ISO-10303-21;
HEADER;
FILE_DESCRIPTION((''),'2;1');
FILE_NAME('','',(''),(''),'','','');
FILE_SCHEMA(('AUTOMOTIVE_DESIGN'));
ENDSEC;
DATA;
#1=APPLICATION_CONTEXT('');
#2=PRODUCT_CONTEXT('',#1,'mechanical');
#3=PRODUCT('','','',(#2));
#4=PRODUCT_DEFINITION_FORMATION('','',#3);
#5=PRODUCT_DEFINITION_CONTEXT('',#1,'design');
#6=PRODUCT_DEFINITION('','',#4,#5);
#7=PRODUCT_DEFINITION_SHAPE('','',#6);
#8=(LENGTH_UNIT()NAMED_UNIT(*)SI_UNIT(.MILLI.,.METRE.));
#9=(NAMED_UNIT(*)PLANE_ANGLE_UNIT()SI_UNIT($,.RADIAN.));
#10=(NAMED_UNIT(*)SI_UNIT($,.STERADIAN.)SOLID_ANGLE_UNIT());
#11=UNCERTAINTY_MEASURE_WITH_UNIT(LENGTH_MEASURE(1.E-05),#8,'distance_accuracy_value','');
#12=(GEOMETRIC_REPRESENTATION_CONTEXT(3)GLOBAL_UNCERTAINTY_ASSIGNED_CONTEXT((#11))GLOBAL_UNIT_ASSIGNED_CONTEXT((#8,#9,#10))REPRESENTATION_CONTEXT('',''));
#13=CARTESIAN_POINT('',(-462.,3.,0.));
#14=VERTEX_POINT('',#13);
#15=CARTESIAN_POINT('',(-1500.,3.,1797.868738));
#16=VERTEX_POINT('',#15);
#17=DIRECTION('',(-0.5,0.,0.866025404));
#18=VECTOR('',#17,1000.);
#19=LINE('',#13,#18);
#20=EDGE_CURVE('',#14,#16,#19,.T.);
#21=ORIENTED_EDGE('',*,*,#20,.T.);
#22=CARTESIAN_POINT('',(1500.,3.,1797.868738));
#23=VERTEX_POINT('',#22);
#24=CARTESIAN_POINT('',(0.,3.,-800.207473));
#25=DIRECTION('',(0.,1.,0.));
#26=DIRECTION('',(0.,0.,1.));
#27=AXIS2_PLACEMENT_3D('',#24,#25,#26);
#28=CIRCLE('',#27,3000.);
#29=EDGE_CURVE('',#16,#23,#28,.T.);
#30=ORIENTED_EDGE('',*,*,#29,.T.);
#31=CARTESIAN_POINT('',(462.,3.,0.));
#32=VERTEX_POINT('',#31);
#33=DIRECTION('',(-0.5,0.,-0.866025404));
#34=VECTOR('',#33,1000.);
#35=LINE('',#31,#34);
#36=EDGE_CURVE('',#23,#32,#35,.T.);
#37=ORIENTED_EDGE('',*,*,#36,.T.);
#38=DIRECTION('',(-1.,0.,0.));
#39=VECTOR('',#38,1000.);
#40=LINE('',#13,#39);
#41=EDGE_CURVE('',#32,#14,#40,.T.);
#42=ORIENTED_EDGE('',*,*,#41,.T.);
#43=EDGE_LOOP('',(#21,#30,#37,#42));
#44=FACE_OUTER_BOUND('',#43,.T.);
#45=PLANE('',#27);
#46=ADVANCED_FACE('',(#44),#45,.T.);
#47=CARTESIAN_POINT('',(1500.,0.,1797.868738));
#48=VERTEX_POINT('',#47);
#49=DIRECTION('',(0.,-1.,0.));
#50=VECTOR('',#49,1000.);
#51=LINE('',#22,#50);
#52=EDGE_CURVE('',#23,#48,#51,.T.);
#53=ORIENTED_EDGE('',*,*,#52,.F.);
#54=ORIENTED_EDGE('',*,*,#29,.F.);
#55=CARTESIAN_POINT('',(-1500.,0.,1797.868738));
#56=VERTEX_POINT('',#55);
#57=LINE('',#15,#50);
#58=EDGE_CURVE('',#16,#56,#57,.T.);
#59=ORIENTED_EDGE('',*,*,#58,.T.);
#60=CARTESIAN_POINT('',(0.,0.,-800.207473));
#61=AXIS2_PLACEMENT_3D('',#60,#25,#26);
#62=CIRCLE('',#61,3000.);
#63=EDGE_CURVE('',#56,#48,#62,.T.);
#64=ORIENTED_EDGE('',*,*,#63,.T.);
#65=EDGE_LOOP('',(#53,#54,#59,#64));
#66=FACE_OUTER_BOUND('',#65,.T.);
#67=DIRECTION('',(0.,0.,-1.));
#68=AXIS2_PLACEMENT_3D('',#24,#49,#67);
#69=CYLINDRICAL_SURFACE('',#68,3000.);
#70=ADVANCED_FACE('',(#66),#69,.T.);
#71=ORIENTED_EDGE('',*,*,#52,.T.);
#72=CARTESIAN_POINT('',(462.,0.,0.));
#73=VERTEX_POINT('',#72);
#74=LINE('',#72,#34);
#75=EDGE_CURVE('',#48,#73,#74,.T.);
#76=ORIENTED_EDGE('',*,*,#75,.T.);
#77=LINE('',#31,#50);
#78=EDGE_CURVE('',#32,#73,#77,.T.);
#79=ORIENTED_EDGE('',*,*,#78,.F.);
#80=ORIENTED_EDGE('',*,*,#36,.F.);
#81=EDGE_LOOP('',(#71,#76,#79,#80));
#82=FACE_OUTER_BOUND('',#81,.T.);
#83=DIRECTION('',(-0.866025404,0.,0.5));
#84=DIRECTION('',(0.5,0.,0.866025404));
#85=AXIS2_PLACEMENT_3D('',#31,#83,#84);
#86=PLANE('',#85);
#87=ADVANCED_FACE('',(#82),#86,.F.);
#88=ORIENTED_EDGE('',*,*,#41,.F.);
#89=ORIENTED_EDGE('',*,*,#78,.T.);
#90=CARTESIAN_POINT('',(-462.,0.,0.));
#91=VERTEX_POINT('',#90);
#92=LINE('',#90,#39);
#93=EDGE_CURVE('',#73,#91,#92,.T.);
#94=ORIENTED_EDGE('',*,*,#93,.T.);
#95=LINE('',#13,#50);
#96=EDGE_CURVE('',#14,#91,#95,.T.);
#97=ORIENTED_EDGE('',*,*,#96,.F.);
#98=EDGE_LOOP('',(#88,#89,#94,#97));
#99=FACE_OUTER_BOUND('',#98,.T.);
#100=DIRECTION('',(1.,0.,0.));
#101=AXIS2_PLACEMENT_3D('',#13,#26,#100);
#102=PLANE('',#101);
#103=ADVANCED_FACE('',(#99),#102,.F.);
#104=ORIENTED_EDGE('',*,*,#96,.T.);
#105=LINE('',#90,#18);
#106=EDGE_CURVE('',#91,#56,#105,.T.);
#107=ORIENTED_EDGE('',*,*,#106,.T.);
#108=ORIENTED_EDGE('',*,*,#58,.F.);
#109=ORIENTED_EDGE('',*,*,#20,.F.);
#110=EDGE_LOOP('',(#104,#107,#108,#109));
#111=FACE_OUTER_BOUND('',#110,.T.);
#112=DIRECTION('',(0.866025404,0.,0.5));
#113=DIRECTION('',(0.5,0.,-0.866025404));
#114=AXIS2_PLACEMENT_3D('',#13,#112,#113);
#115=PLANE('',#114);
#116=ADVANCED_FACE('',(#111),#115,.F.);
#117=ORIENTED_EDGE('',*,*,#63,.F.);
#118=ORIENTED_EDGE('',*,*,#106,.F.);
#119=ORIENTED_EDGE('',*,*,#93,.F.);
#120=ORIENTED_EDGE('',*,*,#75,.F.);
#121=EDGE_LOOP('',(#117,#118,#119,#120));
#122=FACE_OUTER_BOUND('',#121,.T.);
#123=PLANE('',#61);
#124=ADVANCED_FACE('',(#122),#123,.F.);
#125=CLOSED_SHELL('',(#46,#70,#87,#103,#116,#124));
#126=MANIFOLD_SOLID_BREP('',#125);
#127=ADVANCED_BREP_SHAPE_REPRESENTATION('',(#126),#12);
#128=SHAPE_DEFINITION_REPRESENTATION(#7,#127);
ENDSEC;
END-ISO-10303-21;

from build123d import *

# Parameters (mm, degrees)
BOSS_EXTRUDE1_DEPTH = 3


with BuildPart() as part:
    # Sketch1 → Boss-Extrude1 (new body)
    with BuildSketch(Plane(origin=(0, 0, 0), x_dir=(1, 0, 0), z_dir=(0, 1, 0))):
        with BuildLine():
            Line((-462, 0), (462, 0))
            Line((462, 0), (1500, -1797.868738256))
            ThreePointArc((1500, -1797.868738256), (0, -2199.792526903), (-1500, -1797.868738256))
            Line((-1500, -1797.868738256), (-462, 0))
        make_face()
    extrude(amount=BOSS_EXTRUDE1_DEPTH)


solid = part.part
